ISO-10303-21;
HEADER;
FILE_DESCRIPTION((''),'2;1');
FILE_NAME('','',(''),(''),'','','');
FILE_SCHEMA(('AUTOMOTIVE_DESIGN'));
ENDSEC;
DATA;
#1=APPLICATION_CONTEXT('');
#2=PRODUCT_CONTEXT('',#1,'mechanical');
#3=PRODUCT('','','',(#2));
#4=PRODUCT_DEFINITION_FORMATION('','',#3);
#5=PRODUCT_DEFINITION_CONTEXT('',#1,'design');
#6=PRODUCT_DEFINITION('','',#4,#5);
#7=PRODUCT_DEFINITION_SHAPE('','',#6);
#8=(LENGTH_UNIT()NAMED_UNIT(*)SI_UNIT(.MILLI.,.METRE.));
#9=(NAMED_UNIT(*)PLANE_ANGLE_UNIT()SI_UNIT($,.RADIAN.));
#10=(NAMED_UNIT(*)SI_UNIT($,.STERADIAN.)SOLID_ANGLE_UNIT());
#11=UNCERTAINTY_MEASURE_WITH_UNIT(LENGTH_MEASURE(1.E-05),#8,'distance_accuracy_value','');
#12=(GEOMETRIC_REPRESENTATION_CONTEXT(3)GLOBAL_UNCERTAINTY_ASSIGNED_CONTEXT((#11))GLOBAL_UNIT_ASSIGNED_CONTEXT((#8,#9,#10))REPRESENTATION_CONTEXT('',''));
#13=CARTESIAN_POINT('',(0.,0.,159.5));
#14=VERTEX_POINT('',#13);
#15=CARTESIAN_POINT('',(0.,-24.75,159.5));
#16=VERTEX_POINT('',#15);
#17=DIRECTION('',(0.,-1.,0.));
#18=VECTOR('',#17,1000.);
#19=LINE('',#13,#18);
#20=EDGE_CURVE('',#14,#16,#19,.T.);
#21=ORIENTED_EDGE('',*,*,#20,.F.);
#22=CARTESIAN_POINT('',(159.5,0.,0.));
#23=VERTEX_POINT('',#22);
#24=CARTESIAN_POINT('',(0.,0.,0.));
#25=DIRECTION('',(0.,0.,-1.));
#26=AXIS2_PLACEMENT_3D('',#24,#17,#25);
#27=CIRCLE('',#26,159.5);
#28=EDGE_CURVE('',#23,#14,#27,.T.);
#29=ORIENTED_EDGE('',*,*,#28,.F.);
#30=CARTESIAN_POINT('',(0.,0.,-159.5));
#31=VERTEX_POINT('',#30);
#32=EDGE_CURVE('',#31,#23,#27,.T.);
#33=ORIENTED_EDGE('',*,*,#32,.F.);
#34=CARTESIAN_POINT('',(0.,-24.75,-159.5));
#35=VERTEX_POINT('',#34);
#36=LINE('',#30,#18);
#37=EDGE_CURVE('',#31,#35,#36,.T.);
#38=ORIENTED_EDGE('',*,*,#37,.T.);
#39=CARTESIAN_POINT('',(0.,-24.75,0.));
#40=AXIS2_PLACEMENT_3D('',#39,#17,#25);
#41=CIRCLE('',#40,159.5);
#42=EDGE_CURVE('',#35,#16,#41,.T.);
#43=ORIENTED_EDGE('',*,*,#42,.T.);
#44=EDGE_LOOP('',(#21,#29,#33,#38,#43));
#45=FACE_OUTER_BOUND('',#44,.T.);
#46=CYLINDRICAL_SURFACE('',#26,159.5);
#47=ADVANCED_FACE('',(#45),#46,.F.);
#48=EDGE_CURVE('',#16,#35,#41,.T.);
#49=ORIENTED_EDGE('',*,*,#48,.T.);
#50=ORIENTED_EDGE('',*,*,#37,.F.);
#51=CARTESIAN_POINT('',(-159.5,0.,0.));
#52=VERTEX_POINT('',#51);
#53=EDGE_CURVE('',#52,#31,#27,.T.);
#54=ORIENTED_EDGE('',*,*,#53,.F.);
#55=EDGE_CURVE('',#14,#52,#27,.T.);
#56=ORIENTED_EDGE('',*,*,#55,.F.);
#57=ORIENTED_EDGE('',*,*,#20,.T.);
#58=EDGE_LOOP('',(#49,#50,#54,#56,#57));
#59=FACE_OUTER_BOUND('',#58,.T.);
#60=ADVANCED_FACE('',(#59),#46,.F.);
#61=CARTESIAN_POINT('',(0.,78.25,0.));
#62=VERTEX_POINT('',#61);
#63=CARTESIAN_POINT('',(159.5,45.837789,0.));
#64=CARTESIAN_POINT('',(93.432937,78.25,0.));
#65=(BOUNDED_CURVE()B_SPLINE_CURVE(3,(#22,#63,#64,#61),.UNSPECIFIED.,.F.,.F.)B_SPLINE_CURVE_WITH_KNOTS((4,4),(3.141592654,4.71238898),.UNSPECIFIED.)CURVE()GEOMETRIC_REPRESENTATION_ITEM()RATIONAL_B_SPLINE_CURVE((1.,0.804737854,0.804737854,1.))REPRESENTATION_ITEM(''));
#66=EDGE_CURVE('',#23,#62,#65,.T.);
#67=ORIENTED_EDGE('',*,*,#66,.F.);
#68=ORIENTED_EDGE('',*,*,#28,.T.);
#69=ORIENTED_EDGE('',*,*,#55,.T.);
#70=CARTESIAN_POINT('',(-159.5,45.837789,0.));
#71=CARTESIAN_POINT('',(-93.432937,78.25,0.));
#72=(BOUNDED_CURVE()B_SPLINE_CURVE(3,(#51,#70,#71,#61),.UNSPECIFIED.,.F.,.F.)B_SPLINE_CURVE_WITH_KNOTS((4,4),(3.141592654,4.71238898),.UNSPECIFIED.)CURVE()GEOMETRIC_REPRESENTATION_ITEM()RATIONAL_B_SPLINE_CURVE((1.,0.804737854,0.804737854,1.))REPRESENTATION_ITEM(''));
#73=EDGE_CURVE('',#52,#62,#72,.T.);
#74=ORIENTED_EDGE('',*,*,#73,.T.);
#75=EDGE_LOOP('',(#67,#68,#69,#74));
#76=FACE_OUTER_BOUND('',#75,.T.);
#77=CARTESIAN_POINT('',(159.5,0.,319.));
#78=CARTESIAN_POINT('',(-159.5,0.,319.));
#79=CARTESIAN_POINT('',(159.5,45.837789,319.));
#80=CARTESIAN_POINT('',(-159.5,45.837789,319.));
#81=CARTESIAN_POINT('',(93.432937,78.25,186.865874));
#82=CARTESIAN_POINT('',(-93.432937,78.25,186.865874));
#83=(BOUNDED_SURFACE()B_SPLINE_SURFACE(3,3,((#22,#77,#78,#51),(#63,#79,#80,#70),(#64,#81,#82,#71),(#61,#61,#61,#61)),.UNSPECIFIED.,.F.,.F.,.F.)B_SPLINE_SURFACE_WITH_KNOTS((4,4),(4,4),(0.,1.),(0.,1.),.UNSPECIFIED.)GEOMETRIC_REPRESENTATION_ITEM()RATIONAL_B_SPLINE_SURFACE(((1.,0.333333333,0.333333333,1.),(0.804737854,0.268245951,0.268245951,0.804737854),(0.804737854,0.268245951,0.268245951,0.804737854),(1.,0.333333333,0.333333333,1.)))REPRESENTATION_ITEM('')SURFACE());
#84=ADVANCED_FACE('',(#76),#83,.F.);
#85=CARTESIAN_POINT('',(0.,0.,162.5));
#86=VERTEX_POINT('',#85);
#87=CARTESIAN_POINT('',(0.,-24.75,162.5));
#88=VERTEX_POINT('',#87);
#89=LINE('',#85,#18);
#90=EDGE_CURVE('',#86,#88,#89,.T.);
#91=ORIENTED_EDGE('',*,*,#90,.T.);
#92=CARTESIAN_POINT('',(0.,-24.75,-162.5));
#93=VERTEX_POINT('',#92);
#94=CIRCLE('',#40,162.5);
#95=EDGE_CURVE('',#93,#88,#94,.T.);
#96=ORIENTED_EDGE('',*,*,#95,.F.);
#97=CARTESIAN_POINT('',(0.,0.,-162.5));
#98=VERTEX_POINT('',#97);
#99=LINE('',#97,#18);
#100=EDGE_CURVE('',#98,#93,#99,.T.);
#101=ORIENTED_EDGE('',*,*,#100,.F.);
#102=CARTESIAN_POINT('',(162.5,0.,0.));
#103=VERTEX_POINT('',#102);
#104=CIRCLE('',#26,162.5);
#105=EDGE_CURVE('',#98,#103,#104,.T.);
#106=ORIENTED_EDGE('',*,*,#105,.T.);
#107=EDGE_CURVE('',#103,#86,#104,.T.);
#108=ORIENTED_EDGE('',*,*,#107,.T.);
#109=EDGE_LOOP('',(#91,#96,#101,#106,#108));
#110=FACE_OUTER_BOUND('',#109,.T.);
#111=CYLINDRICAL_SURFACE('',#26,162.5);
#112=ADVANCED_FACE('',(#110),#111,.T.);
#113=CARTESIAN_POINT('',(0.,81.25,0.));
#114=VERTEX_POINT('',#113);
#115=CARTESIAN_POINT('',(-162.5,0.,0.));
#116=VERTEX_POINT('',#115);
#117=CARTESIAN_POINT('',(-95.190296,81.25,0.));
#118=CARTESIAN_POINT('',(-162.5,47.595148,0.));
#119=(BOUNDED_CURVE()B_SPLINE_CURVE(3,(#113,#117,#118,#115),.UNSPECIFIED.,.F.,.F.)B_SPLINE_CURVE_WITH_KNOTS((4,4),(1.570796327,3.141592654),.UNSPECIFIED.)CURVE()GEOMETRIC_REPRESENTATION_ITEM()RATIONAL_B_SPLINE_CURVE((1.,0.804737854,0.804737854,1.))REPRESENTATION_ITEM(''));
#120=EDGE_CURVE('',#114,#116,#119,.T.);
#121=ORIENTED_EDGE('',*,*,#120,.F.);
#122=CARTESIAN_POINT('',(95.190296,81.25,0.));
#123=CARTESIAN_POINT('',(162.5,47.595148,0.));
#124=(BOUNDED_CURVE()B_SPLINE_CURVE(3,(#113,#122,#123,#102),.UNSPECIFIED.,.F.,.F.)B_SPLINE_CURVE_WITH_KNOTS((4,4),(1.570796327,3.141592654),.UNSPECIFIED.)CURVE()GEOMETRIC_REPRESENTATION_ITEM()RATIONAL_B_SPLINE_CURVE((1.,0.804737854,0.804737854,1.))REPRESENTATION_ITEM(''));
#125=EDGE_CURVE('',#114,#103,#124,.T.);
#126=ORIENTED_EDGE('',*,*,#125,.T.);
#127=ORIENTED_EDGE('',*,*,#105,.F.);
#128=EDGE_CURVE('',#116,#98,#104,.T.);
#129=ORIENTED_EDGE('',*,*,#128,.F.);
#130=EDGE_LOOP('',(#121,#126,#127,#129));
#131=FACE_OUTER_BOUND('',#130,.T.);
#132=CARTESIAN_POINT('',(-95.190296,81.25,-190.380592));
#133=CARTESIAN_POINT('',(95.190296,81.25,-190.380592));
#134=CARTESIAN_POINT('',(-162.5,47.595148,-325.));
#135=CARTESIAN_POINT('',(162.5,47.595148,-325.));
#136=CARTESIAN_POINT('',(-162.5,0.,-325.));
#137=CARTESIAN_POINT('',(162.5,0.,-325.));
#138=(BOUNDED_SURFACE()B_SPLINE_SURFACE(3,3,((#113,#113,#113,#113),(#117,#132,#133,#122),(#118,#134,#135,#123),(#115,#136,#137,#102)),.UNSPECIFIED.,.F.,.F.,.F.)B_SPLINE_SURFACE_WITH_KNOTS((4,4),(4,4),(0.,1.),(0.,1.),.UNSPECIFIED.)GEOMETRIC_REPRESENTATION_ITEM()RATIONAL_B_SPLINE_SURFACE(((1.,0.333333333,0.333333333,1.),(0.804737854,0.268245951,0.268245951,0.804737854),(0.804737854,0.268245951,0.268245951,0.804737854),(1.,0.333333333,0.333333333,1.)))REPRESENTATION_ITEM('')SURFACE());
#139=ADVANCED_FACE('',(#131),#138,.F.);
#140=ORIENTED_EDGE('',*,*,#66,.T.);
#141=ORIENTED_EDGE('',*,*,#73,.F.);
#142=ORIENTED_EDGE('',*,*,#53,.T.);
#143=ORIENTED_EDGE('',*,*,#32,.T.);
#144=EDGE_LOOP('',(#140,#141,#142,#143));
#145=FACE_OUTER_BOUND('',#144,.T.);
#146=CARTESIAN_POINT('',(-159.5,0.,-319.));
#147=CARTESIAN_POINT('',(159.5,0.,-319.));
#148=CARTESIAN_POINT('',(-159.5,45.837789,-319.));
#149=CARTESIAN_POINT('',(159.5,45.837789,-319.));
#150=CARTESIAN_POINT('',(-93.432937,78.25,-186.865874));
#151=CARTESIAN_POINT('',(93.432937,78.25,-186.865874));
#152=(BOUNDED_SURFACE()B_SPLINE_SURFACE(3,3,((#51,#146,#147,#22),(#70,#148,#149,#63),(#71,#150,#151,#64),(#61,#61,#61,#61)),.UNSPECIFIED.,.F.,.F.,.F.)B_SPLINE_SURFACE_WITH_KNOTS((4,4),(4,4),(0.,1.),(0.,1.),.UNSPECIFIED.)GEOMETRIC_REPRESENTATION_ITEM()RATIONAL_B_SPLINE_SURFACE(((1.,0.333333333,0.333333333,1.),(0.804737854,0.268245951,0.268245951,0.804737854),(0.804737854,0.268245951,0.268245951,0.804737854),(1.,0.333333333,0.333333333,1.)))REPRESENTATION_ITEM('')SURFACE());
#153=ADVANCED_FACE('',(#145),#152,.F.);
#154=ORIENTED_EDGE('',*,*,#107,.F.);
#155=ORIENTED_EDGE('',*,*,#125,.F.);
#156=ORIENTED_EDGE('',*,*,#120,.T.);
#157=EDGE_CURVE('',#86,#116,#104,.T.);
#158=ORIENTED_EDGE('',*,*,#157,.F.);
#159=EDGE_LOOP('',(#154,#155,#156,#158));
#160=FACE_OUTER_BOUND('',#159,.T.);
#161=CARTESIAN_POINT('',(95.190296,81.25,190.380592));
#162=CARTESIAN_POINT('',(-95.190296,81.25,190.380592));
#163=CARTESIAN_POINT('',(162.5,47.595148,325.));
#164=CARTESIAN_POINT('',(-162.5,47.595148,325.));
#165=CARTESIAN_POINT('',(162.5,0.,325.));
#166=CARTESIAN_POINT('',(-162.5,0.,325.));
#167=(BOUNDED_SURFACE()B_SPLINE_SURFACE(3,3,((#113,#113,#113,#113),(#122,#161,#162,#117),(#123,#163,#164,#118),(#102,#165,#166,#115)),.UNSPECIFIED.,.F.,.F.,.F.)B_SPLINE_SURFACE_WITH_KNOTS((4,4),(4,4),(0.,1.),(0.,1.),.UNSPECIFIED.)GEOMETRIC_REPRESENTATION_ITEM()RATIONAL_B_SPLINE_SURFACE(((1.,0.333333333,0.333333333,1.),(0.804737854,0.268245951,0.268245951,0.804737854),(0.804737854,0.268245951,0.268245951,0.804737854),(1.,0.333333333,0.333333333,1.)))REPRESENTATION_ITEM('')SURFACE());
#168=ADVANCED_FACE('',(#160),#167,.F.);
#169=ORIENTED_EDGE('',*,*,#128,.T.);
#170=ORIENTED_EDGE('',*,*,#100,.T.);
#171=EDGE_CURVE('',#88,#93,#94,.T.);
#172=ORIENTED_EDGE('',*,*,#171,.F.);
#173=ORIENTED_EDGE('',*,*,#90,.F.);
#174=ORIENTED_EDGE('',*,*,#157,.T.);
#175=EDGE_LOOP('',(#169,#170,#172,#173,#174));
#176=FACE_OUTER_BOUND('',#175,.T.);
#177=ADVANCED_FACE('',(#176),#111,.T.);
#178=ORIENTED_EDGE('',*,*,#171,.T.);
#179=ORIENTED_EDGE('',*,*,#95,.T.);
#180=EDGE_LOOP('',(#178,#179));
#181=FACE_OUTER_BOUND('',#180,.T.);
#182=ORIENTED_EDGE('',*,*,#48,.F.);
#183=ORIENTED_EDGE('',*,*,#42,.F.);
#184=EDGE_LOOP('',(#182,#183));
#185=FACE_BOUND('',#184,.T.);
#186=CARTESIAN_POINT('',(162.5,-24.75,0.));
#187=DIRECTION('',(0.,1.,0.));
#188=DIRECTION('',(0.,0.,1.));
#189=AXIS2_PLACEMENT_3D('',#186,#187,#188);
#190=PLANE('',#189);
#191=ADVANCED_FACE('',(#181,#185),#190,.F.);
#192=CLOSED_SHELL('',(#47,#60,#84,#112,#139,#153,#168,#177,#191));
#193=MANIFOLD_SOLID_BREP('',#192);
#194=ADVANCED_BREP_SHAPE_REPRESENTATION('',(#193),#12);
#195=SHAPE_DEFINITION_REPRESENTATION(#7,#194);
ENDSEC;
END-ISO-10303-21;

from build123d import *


with BuildPart() as part:
    # Sketch3 → Revolve2 (revolve)
    with BuildSketch(Plane.XY, mode=Mode.PRIVATE) as revolve2_sk:
        with BuildLine():
            Line((-162.5, 0), (-162.5, -24.75))
            Line((-162.5, -24.75), (-159.5, -24.75))
            Line((-159.5, -24.75), (-159.5, 0))
            add(Edge.make_bspline(
                [(0, 78.25), (-159.5, 78.25), (-159.5, 0)],
                knots=[1.570796327, 1.570796327, 1.570796327, 3.141592654, 3.141592654, 3.141592654], degree=2, weights=[1, 0.707106781, 1]))
            Line((0, 78.25), (0, 81.25))
            add(Edge.make_bspline(
                [(0, 81.25), (-162.5, 81.25), (-162.5, 0)],
                knots=[1.570796327, 1.570796327, 1.570796327, 3.141592654, 3.141592654, 3.141592654], degree=2, weights=[1, 0.707106781, 1]))
        make_face()
    revolve(revolve2_sk.sketch.rotate(Axis((0, 0, 0), (0, 1, 0)), 270), axis=Axis((0, 0, 0), (0, 1, 0)))


solid = part.part
